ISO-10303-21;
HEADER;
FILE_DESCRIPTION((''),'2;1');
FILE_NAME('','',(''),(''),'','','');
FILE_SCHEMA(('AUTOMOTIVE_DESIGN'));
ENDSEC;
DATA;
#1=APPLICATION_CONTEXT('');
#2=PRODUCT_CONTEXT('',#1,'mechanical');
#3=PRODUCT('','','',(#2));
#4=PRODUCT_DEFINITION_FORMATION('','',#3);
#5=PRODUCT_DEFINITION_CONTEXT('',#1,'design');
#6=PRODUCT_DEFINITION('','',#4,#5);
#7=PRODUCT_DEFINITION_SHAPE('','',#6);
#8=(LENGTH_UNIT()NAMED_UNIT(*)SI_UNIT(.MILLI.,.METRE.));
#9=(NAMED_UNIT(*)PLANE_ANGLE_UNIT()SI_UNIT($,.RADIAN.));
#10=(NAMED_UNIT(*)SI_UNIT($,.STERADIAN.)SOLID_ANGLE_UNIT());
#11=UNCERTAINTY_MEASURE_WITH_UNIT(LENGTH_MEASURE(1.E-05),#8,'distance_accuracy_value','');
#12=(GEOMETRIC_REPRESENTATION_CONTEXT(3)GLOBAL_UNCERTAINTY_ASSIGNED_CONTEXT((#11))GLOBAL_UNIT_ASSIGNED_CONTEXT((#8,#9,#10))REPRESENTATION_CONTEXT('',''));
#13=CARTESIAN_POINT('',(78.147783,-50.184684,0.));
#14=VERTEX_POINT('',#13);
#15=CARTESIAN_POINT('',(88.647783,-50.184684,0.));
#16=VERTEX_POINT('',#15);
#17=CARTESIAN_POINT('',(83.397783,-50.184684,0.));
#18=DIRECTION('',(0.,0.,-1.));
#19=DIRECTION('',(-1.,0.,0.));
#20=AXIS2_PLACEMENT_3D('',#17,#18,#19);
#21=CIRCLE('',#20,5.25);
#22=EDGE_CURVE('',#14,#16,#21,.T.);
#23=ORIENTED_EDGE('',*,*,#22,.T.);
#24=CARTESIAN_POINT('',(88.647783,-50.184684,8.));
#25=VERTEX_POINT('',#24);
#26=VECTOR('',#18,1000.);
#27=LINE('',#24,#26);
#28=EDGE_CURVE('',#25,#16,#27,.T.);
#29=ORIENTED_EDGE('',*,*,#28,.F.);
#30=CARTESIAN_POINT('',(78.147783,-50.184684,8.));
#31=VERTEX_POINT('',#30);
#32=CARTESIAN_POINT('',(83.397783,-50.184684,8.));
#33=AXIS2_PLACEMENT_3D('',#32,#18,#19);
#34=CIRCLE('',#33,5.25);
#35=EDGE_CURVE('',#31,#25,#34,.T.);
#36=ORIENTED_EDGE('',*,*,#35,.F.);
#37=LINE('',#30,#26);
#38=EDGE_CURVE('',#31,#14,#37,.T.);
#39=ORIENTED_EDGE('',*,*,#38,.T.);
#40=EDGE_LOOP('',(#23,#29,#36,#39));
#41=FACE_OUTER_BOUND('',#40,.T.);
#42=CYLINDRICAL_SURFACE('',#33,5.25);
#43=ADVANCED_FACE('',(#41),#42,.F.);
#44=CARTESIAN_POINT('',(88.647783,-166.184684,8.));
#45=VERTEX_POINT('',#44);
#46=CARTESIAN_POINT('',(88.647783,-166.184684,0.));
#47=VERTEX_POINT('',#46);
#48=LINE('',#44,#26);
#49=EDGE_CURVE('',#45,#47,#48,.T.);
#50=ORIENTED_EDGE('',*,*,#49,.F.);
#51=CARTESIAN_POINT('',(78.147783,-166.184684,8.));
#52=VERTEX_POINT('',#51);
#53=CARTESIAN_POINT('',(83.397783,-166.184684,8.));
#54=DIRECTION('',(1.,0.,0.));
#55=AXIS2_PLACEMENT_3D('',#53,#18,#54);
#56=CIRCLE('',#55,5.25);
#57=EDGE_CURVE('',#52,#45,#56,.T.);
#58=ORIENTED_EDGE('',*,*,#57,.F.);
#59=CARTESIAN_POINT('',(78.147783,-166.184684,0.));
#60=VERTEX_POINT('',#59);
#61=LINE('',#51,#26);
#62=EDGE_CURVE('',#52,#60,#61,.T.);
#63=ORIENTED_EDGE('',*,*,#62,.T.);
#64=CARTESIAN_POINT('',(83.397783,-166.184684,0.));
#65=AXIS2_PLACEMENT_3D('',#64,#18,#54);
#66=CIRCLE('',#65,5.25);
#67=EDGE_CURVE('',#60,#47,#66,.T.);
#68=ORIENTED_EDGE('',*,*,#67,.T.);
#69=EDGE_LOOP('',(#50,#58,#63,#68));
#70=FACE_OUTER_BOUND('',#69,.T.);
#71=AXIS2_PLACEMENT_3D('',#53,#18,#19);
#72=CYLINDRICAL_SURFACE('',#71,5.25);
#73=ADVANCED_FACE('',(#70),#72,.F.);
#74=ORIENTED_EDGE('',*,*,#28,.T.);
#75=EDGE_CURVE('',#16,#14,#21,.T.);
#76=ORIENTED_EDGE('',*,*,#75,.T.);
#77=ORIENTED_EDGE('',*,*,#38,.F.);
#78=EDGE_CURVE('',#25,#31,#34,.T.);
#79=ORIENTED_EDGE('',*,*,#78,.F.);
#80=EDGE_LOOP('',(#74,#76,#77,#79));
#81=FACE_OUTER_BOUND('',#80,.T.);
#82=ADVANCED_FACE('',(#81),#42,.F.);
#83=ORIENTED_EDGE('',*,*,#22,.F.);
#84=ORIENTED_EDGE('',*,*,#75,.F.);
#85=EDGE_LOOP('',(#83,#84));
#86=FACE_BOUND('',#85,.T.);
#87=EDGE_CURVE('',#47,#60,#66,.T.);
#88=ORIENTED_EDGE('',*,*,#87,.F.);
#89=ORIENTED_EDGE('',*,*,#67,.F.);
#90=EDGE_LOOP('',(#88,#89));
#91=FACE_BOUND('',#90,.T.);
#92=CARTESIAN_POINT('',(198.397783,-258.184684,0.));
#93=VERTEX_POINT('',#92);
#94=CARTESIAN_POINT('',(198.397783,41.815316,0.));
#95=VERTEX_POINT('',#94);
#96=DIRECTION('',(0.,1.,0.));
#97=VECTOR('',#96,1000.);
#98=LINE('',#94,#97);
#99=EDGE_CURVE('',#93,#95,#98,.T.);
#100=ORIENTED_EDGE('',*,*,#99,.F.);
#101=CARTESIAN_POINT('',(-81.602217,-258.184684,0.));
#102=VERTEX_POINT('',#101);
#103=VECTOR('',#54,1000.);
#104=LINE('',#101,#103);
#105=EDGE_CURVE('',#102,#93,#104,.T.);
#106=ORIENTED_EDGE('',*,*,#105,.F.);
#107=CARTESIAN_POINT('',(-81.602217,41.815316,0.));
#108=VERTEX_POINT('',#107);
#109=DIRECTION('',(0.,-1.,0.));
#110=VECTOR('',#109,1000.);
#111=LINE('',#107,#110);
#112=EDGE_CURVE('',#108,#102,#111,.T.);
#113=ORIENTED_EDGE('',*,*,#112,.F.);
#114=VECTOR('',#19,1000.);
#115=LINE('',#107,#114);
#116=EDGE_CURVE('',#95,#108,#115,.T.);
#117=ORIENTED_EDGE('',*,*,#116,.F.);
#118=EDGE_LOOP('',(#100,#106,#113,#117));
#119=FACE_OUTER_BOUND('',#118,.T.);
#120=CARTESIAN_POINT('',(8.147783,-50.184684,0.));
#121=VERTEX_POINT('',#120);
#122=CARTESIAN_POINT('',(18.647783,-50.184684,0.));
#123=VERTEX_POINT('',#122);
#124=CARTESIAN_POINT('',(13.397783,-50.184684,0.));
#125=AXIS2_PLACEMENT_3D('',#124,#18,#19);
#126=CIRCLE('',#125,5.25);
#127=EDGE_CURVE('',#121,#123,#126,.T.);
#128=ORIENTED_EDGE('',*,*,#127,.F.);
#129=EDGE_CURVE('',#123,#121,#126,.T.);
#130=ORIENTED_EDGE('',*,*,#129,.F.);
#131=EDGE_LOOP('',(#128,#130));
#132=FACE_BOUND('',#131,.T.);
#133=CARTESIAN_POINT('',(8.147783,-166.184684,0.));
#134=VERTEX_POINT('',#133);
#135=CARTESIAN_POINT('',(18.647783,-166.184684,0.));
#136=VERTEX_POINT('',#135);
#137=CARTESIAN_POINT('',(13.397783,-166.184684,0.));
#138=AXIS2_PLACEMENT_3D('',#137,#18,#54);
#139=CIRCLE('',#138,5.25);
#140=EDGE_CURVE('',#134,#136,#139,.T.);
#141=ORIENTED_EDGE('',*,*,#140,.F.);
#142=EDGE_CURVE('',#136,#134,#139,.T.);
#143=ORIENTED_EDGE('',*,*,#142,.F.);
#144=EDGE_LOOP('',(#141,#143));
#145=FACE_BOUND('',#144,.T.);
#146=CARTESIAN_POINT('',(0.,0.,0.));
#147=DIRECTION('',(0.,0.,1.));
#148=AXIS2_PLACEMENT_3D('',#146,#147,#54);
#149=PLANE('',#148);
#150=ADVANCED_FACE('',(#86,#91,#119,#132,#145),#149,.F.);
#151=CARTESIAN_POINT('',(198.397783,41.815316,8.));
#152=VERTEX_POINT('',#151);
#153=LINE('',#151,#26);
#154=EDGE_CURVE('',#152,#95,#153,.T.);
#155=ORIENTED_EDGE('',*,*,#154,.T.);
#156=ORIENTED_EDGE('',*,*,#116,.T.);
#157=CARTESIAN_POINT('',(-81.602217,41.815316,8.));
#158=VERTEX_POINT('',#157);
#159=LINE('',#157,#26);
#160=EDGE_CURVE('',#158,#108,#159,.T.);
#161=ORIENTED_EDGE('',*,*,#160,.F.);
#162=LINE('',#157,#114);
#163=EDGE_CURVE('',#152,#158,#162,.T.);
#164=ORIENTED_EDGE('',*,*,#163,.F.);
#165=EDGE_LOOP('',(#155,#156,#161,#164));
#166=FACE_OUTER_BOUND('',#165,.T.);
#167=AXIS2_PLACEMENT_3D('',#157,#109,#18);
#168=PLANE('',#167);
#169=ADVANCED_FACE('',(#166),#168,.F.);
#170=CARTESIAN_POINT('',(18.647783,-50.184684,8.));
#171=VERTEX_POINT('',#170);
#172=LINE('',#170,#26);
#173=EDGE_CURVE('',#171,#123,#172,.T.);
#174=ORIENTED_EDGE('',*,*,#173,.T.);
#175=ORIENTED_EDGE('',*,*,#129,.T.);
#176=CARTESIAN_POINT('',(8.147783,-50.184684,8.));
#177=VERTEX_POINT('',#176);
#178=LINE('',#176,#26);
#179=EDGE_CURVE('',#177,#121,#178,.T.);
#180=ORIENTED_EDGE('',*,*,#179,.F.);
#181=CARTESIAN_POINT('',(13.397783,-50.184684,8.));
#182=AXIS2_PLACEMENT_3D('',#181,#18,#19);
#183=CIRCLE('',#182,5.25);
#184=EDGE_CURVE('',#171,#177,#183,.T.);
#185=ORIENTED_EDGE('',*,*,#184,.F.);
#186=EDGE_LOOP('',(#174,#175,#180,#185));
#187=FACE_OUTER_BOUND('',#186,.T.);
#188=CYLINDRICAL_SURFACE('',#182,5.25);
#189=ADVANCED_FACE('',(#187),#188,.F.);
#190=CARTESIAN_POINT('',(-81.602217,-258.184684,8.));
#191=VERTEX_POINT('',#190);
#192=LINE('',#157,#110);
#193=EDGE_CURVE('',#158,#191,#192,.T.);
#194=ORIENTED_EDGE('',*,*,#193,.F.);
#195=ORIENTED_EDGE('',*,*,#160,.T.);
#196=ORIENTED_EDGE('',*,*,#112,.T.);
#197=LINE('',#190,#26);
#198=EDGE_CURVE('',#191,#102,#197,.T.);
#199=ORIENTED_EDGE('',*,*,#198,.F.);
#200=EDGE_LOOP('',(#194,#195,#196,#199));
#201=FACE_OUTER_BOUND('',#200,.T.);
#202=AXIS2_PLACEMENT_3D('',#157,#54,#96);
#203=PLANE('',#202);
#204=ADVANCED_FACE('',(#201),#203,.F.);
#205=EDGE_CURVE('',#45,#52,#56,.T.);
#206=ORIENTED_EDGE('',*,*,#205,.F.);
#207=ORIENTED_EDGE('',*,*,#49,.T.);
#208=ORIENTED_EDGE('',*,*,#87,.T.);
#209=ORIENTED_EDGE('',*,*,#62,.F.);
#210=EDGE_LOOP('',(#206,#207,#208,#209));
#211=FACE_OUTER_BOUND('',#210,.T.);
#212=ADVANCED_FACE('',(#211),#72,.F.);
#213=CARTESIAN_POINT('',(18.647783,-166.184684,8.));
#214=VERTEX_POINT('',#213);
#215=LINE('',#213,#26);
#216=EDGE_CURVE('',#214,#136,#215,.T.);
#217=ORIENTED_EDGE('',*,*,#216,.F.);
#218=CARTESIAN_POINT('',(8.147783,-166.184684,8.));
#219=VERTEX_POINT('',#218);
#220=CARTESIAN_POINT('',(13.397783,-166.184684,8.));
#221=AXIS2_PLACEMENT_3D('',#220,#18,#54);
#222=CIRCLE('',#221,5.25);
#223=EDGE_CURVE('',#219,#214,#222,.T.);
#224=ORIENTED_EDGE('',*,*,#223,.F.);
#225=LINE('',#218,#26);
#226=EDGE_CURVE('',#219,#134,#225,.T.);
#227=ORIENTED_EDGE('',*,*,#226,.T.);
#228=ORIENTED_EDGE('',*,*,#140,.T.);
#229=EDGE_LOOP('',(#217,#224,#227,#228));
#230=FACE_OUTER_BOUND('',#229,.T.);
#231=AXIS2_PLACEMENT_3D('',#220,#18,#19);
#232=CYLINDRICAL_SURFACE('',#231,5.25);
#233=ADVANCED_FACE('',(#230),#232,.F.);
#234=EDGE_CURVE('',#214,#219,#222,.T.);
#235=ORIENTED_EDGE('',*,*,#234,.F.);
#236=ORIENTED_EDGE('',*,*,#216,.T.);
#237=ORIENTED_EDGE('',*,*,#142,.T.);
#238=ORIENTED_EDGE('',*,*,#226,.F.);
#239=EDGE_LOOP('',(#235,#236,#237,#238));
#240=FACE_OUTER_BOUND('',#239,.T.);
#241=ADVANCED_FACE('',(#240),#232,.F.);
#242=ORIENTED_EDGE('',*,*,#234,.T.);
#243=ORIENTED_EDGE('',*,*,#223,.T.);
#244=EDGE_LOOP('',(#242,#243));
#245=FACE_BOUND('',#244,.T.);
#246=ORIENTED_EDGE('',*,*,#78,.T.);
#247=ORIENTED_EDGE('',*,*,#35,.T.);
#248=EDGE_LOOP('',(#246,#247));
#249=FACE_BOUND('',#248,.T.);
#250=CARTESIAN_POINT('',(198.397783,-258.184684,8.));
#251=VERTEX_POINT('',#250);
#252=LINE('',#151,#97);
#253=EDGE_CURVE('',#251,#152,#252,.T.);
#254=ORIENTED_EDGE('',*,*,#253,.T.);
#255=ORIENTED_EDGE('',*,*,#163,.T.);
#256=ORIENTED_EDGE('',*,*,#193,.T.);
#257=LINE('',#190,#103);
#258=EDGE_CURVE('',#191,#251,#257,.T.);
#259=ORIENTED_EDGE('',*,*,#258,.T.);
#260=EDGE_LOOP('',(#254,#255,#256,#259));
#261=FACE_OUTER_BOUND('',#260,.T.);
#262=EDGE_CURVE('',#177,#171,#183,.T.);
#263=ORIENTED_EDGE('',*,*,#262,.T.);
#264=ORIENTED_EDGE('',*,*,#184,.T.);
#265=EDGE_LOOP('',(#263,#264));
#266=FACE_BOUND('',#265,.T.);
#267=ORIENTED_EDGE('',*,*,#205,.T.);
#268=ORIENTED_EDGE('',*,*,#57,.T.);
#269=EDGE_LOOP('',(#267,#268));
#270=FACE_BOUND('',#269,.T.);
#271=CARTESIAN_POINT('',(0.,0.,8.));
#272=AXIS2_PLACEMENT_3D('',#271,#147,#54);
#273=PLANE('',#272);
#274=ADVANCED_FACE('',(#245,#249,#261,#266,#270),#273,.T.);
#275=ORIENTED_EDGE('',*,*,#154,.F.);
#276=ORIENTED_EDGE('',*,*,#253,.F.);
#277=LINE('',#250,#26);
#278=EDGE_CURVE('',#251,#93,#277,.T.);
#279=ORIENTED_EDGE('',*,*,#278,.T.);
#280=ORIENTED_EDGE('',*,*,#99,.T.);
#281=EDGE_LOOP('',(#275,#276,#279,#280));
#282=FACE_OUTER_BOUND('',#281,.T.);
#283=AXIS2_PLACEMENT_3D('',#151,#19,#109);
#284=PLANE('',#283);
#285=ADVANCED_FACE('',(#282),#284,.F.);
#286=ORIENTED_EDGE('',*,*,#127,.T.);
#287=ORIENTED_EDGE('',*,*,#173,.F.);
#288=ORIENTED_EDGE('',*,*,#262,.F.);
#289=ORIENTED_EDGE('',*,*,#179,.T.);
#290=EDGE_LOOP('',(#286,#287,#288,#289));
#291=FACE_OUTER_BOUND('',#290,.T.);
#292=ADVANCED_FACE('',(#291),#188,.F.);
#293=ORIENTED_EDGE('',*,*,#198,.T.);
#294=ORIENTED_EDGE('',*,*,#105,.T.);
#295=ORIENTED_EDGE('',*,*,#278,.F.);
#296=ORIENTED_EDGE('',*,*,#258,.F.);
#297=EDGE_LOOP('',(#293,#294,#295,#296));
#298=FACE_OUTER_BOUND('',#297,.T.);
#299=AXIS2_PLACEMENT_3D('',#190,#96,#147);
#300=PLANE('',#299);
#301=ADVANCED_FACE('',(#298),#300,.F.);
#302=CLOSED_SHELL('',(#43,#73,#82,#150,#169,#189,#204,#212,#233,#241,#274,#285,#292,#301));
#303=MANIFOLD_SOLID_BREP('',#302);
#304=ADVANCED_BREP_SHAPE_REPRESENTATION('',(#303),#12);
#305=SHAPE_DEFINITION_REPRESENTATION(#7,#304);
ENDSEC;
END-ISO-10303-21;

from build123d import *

# Parameters (mm, degrees)
SKETCH1_W           = 280
SKETCH1_H           = 300
BOSS_EXTRUDE1_DEPTH = 8
SKETCH2_R           = 5.25
CUT_EXTRUDE1_DEPTH  = 326.70694063


with BuildPart() as part:
    # Sketch1 → Boss-Extrude1 (new body)
    with BuildSketch(Plane.XY):
        with Locations((58.397782613, -108.184683955)):
            Rectangle(SKETCH1_W, SKETCH1_H)
    extrude(amount=BOSS_EXTRUDE1_DEPTH)

    # Sketch2 → Cut-Extrude1 (cut, through all)
    with BuildSketch(Plane(origin=(0, 0, 0), x_dir=(-1, 0, 0), z_dir=(0, 0, -1))):
        with Locations((-13.397782613, -50.184683955)):
            Circle(SKETCH2_R)
        with Locations((-83.397782613, -50.184683955)):
            Circle(SKETCH2_R)
        with Locations(Location((-13.397782613, -166.184683955, 0), (0, 0, 180))):
            Circle(SKETCH2_R)
        with Locations(Location((-83.397782613, -166.184683955, 0), (0, 0, 180))):
            Circle(SKETCH2_R)
    extrude(amount=-CUT_EXTRUDE1_DEPTH, mode=Mode.SUBTRACT)


solid = part.part
